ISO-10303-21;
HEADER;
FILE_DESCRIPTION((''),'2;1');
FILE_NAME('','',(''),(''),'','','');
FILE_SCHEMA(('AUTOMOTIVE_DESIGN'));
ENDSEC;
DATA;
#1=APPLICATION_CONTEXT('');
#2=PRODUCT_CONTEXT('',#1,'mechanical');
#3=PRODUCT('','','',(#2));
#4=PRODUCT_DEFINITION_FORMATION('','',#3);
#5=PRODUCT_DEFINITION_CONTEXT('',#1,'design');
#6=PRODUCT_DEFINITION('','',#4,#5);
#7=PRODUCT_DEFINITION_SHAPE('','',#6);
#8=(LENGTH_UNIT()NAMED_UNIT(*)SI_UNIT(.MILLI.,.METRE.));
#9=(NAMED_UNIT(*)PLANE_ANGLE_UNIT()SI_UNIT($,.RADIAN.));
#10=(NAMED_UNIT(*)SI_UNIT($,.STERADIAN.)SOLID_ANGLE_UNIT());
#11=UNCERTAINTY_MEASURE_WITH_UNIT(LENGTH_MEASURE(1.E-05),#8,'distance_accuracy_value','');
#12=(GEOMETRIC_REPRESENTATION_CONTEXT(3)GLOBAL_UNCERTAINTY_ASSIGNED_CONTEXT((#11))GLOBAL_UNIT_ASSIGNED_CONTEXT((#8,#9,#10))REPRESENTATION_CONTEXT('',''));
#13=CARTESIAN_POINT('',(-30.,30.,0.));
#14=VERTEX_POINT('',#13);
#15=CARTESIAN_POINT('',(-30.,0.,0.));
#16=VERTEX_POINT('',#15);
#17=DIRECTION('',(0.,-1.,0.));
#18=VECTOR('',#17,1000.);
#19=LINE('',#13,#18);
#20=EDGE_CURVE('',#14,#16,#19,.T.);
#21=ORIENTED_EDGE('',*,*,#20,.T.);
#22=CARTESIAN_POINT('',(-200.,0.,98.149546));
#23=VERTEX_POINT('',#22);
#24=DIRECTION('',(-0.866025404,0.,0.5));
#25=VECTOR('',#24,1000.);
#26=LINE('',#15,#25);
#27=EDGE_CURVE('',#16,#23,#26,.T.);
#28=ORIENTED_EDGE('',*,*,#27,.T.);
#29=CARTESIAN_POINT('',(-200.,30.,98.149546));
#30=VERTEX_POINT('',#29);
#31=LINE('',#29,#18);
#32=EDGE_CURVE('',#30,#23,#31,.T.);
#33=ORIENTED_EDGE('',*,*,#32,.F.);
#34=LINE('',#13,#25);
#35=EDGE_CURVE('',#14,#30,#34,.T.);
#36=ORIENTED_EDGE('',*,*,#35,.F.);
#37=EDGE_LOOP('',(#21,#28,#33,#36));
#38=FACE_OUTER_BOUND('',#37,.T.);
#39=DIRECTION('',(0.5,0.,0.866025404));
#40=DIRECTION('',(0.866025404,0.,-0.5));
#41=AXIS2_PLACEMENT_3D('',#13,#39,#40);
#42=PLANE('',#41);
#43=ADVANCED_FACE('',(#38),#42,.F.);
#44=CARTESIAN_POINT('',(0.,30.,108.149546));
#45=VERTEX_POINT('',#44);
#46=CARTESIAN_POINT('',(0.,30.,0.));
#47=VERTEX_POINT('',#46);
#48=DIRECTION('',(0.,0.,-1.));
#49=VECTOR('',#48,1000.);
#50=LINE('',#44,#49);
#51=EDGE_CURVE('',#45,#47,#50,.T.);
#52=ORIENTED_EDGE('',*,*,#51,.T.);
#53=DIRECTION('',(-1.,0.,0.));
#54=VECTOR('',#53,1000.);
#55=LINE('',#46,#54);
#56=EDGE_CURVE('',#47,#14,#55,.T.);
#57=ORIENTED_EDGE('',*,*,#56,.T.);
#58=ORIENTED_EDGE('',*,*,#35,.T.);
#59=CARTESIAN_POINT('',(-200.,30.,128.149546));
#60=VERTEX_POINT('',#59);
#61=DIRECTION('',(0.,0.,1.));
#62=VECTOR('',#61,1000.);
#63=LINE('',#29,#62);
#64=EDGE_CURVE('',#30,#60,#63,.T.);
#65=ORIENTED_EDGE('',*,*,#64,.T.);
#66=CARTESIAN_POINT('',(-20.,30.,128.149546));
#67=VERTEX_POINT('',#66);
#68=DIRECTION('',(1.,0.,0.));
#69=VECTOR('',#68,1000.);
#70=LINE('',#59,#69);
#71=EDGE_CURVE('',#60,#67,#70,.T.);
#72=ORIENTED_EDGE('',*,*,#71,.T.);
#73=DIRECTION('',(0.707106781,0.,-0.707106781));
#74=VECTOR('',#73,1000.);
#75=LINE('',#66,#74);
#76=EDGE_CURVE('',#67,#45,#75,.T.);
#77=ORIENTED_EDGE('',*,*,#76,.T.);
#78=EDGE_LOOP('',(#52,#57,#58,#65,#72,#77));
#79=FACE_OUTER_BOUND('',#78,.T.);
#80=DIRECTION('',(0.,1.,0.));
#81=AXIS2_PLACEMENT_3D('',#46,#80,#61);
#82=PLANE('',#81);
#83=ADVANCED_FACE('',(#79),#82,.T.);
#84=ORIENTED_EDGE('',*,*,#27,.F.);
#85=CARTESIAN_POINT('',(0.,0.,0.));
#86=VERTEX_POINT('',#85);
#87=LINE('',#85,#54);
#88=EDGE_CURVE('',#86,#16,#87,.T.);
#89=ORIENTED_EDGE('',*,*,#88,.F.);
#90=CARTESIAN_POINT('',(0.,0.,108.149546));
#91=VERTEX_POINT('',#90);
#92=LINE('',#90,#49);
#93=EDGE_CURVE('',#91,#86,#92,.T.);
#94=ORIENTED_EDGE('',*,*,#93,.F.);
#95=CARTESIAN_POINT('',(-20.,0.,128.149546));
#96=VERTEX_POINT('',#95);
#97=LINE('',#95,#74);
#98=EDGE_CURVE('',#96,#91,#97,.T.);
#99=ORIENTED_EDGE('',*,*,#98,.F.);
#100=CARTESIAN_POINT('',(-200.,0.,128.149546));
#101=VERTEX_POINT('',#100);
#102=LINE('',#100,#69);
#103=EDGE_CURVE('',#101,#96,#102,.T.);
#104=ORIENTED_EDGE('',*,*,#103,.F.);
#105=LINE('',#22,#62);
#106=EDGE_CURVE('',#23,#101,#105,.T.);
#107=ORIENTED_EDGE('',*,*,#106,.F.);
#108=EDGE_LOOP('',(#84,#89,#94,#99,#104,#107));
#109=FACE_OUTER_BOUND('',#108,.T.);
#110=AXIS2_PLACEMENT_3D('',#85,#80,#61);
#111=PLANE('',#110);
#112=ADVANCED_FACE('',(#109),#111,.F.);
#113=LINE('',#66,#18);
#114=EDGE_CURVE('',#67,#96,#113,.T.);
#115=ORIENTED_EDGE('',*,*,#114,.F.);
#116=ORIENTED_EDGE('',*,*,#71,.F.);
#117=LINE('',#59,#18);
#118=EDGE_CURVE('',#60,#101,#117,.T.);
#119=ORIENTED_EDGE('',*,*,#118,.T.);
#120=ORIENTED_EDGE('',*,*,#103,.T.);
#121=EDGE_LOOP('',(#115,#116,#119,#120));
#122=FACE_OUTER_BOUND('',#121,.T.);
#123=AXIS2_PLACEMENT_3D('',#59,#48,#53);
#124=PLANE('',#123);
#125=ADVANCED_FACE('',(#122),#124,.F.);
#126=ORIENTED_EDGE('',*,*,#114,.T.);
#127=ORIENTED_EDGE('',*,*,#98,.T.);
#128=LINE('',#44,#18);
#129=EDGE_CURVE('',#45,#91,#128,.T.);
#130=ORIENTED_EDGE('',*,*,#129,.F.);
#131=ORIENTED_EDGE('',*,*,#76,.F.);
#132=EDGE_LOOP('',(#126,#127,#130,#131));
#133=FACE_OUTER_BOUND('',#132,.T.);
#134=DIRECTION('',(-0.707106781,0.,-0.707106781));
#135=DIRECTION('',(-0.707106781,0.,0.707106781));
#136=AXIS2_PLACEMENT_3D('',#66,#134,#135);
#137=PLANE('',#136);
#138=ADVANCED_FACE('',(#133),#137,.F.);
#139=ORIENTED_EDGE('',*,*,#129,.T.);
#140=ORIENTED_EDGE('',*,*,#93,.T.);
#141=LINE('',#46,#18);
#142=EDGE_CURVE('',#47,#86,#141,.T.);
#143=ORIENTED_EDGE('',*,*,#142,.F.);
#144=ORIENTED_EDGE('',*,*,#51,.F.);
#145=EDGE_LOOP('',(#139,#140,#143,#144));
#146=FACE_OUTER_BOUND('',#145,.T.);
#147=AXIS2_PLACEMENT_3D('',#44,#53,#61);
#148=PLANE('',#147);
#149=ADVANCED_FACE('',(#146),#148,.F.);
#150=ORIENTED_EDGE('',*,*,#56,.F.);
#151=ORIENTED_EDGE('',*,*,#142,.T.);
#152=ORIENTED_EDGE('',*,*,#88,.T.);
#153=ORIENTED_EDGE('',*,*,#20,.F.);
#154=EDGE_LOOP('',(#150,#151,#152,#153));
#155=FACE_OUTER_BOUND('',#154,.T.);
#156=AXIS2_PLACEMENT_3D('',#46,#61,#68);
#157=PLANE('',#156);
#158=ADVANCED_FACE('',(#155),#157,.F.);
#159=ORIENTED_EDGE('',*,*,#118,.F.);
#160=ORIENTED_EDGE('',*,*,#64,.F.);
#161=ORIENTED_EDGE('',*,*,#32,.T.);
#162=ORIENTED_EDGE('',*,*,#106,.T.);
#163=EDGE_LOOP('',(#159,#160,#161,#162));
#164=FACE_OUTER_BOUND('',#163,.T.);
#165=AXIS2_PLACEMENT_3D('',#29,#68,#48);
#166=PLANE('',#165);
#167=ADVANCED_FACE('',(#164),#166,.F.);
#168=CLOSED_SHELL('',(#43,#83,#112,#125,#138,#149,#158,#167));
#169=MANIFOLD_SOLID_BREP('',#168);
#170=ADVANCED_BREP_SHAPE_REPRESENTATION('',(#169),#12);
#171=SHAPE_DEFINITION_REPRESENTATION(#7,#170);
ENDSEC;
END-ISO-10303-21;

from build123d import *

# Parameters (mm, degrees)
EXTRUDE_1_DEPTH = 30


with BuildPart() as part:
    # 草图1 → 凸台-拉伸1 (new body)
    with BuildSketch(Plane(origin=(0, 0, 0), x_dir=(1, 0, 0), z_dir=(0, 1, 0))):
        Polygon((0, 0), (-30, 0), (-200, -98.149545762), (-200, -128.149545762), (-20, -128.149545762), (0, -108.149545762), align=None)
    extrude(amount=EXTRUDE_1_DEPTH)


solid = part.part
